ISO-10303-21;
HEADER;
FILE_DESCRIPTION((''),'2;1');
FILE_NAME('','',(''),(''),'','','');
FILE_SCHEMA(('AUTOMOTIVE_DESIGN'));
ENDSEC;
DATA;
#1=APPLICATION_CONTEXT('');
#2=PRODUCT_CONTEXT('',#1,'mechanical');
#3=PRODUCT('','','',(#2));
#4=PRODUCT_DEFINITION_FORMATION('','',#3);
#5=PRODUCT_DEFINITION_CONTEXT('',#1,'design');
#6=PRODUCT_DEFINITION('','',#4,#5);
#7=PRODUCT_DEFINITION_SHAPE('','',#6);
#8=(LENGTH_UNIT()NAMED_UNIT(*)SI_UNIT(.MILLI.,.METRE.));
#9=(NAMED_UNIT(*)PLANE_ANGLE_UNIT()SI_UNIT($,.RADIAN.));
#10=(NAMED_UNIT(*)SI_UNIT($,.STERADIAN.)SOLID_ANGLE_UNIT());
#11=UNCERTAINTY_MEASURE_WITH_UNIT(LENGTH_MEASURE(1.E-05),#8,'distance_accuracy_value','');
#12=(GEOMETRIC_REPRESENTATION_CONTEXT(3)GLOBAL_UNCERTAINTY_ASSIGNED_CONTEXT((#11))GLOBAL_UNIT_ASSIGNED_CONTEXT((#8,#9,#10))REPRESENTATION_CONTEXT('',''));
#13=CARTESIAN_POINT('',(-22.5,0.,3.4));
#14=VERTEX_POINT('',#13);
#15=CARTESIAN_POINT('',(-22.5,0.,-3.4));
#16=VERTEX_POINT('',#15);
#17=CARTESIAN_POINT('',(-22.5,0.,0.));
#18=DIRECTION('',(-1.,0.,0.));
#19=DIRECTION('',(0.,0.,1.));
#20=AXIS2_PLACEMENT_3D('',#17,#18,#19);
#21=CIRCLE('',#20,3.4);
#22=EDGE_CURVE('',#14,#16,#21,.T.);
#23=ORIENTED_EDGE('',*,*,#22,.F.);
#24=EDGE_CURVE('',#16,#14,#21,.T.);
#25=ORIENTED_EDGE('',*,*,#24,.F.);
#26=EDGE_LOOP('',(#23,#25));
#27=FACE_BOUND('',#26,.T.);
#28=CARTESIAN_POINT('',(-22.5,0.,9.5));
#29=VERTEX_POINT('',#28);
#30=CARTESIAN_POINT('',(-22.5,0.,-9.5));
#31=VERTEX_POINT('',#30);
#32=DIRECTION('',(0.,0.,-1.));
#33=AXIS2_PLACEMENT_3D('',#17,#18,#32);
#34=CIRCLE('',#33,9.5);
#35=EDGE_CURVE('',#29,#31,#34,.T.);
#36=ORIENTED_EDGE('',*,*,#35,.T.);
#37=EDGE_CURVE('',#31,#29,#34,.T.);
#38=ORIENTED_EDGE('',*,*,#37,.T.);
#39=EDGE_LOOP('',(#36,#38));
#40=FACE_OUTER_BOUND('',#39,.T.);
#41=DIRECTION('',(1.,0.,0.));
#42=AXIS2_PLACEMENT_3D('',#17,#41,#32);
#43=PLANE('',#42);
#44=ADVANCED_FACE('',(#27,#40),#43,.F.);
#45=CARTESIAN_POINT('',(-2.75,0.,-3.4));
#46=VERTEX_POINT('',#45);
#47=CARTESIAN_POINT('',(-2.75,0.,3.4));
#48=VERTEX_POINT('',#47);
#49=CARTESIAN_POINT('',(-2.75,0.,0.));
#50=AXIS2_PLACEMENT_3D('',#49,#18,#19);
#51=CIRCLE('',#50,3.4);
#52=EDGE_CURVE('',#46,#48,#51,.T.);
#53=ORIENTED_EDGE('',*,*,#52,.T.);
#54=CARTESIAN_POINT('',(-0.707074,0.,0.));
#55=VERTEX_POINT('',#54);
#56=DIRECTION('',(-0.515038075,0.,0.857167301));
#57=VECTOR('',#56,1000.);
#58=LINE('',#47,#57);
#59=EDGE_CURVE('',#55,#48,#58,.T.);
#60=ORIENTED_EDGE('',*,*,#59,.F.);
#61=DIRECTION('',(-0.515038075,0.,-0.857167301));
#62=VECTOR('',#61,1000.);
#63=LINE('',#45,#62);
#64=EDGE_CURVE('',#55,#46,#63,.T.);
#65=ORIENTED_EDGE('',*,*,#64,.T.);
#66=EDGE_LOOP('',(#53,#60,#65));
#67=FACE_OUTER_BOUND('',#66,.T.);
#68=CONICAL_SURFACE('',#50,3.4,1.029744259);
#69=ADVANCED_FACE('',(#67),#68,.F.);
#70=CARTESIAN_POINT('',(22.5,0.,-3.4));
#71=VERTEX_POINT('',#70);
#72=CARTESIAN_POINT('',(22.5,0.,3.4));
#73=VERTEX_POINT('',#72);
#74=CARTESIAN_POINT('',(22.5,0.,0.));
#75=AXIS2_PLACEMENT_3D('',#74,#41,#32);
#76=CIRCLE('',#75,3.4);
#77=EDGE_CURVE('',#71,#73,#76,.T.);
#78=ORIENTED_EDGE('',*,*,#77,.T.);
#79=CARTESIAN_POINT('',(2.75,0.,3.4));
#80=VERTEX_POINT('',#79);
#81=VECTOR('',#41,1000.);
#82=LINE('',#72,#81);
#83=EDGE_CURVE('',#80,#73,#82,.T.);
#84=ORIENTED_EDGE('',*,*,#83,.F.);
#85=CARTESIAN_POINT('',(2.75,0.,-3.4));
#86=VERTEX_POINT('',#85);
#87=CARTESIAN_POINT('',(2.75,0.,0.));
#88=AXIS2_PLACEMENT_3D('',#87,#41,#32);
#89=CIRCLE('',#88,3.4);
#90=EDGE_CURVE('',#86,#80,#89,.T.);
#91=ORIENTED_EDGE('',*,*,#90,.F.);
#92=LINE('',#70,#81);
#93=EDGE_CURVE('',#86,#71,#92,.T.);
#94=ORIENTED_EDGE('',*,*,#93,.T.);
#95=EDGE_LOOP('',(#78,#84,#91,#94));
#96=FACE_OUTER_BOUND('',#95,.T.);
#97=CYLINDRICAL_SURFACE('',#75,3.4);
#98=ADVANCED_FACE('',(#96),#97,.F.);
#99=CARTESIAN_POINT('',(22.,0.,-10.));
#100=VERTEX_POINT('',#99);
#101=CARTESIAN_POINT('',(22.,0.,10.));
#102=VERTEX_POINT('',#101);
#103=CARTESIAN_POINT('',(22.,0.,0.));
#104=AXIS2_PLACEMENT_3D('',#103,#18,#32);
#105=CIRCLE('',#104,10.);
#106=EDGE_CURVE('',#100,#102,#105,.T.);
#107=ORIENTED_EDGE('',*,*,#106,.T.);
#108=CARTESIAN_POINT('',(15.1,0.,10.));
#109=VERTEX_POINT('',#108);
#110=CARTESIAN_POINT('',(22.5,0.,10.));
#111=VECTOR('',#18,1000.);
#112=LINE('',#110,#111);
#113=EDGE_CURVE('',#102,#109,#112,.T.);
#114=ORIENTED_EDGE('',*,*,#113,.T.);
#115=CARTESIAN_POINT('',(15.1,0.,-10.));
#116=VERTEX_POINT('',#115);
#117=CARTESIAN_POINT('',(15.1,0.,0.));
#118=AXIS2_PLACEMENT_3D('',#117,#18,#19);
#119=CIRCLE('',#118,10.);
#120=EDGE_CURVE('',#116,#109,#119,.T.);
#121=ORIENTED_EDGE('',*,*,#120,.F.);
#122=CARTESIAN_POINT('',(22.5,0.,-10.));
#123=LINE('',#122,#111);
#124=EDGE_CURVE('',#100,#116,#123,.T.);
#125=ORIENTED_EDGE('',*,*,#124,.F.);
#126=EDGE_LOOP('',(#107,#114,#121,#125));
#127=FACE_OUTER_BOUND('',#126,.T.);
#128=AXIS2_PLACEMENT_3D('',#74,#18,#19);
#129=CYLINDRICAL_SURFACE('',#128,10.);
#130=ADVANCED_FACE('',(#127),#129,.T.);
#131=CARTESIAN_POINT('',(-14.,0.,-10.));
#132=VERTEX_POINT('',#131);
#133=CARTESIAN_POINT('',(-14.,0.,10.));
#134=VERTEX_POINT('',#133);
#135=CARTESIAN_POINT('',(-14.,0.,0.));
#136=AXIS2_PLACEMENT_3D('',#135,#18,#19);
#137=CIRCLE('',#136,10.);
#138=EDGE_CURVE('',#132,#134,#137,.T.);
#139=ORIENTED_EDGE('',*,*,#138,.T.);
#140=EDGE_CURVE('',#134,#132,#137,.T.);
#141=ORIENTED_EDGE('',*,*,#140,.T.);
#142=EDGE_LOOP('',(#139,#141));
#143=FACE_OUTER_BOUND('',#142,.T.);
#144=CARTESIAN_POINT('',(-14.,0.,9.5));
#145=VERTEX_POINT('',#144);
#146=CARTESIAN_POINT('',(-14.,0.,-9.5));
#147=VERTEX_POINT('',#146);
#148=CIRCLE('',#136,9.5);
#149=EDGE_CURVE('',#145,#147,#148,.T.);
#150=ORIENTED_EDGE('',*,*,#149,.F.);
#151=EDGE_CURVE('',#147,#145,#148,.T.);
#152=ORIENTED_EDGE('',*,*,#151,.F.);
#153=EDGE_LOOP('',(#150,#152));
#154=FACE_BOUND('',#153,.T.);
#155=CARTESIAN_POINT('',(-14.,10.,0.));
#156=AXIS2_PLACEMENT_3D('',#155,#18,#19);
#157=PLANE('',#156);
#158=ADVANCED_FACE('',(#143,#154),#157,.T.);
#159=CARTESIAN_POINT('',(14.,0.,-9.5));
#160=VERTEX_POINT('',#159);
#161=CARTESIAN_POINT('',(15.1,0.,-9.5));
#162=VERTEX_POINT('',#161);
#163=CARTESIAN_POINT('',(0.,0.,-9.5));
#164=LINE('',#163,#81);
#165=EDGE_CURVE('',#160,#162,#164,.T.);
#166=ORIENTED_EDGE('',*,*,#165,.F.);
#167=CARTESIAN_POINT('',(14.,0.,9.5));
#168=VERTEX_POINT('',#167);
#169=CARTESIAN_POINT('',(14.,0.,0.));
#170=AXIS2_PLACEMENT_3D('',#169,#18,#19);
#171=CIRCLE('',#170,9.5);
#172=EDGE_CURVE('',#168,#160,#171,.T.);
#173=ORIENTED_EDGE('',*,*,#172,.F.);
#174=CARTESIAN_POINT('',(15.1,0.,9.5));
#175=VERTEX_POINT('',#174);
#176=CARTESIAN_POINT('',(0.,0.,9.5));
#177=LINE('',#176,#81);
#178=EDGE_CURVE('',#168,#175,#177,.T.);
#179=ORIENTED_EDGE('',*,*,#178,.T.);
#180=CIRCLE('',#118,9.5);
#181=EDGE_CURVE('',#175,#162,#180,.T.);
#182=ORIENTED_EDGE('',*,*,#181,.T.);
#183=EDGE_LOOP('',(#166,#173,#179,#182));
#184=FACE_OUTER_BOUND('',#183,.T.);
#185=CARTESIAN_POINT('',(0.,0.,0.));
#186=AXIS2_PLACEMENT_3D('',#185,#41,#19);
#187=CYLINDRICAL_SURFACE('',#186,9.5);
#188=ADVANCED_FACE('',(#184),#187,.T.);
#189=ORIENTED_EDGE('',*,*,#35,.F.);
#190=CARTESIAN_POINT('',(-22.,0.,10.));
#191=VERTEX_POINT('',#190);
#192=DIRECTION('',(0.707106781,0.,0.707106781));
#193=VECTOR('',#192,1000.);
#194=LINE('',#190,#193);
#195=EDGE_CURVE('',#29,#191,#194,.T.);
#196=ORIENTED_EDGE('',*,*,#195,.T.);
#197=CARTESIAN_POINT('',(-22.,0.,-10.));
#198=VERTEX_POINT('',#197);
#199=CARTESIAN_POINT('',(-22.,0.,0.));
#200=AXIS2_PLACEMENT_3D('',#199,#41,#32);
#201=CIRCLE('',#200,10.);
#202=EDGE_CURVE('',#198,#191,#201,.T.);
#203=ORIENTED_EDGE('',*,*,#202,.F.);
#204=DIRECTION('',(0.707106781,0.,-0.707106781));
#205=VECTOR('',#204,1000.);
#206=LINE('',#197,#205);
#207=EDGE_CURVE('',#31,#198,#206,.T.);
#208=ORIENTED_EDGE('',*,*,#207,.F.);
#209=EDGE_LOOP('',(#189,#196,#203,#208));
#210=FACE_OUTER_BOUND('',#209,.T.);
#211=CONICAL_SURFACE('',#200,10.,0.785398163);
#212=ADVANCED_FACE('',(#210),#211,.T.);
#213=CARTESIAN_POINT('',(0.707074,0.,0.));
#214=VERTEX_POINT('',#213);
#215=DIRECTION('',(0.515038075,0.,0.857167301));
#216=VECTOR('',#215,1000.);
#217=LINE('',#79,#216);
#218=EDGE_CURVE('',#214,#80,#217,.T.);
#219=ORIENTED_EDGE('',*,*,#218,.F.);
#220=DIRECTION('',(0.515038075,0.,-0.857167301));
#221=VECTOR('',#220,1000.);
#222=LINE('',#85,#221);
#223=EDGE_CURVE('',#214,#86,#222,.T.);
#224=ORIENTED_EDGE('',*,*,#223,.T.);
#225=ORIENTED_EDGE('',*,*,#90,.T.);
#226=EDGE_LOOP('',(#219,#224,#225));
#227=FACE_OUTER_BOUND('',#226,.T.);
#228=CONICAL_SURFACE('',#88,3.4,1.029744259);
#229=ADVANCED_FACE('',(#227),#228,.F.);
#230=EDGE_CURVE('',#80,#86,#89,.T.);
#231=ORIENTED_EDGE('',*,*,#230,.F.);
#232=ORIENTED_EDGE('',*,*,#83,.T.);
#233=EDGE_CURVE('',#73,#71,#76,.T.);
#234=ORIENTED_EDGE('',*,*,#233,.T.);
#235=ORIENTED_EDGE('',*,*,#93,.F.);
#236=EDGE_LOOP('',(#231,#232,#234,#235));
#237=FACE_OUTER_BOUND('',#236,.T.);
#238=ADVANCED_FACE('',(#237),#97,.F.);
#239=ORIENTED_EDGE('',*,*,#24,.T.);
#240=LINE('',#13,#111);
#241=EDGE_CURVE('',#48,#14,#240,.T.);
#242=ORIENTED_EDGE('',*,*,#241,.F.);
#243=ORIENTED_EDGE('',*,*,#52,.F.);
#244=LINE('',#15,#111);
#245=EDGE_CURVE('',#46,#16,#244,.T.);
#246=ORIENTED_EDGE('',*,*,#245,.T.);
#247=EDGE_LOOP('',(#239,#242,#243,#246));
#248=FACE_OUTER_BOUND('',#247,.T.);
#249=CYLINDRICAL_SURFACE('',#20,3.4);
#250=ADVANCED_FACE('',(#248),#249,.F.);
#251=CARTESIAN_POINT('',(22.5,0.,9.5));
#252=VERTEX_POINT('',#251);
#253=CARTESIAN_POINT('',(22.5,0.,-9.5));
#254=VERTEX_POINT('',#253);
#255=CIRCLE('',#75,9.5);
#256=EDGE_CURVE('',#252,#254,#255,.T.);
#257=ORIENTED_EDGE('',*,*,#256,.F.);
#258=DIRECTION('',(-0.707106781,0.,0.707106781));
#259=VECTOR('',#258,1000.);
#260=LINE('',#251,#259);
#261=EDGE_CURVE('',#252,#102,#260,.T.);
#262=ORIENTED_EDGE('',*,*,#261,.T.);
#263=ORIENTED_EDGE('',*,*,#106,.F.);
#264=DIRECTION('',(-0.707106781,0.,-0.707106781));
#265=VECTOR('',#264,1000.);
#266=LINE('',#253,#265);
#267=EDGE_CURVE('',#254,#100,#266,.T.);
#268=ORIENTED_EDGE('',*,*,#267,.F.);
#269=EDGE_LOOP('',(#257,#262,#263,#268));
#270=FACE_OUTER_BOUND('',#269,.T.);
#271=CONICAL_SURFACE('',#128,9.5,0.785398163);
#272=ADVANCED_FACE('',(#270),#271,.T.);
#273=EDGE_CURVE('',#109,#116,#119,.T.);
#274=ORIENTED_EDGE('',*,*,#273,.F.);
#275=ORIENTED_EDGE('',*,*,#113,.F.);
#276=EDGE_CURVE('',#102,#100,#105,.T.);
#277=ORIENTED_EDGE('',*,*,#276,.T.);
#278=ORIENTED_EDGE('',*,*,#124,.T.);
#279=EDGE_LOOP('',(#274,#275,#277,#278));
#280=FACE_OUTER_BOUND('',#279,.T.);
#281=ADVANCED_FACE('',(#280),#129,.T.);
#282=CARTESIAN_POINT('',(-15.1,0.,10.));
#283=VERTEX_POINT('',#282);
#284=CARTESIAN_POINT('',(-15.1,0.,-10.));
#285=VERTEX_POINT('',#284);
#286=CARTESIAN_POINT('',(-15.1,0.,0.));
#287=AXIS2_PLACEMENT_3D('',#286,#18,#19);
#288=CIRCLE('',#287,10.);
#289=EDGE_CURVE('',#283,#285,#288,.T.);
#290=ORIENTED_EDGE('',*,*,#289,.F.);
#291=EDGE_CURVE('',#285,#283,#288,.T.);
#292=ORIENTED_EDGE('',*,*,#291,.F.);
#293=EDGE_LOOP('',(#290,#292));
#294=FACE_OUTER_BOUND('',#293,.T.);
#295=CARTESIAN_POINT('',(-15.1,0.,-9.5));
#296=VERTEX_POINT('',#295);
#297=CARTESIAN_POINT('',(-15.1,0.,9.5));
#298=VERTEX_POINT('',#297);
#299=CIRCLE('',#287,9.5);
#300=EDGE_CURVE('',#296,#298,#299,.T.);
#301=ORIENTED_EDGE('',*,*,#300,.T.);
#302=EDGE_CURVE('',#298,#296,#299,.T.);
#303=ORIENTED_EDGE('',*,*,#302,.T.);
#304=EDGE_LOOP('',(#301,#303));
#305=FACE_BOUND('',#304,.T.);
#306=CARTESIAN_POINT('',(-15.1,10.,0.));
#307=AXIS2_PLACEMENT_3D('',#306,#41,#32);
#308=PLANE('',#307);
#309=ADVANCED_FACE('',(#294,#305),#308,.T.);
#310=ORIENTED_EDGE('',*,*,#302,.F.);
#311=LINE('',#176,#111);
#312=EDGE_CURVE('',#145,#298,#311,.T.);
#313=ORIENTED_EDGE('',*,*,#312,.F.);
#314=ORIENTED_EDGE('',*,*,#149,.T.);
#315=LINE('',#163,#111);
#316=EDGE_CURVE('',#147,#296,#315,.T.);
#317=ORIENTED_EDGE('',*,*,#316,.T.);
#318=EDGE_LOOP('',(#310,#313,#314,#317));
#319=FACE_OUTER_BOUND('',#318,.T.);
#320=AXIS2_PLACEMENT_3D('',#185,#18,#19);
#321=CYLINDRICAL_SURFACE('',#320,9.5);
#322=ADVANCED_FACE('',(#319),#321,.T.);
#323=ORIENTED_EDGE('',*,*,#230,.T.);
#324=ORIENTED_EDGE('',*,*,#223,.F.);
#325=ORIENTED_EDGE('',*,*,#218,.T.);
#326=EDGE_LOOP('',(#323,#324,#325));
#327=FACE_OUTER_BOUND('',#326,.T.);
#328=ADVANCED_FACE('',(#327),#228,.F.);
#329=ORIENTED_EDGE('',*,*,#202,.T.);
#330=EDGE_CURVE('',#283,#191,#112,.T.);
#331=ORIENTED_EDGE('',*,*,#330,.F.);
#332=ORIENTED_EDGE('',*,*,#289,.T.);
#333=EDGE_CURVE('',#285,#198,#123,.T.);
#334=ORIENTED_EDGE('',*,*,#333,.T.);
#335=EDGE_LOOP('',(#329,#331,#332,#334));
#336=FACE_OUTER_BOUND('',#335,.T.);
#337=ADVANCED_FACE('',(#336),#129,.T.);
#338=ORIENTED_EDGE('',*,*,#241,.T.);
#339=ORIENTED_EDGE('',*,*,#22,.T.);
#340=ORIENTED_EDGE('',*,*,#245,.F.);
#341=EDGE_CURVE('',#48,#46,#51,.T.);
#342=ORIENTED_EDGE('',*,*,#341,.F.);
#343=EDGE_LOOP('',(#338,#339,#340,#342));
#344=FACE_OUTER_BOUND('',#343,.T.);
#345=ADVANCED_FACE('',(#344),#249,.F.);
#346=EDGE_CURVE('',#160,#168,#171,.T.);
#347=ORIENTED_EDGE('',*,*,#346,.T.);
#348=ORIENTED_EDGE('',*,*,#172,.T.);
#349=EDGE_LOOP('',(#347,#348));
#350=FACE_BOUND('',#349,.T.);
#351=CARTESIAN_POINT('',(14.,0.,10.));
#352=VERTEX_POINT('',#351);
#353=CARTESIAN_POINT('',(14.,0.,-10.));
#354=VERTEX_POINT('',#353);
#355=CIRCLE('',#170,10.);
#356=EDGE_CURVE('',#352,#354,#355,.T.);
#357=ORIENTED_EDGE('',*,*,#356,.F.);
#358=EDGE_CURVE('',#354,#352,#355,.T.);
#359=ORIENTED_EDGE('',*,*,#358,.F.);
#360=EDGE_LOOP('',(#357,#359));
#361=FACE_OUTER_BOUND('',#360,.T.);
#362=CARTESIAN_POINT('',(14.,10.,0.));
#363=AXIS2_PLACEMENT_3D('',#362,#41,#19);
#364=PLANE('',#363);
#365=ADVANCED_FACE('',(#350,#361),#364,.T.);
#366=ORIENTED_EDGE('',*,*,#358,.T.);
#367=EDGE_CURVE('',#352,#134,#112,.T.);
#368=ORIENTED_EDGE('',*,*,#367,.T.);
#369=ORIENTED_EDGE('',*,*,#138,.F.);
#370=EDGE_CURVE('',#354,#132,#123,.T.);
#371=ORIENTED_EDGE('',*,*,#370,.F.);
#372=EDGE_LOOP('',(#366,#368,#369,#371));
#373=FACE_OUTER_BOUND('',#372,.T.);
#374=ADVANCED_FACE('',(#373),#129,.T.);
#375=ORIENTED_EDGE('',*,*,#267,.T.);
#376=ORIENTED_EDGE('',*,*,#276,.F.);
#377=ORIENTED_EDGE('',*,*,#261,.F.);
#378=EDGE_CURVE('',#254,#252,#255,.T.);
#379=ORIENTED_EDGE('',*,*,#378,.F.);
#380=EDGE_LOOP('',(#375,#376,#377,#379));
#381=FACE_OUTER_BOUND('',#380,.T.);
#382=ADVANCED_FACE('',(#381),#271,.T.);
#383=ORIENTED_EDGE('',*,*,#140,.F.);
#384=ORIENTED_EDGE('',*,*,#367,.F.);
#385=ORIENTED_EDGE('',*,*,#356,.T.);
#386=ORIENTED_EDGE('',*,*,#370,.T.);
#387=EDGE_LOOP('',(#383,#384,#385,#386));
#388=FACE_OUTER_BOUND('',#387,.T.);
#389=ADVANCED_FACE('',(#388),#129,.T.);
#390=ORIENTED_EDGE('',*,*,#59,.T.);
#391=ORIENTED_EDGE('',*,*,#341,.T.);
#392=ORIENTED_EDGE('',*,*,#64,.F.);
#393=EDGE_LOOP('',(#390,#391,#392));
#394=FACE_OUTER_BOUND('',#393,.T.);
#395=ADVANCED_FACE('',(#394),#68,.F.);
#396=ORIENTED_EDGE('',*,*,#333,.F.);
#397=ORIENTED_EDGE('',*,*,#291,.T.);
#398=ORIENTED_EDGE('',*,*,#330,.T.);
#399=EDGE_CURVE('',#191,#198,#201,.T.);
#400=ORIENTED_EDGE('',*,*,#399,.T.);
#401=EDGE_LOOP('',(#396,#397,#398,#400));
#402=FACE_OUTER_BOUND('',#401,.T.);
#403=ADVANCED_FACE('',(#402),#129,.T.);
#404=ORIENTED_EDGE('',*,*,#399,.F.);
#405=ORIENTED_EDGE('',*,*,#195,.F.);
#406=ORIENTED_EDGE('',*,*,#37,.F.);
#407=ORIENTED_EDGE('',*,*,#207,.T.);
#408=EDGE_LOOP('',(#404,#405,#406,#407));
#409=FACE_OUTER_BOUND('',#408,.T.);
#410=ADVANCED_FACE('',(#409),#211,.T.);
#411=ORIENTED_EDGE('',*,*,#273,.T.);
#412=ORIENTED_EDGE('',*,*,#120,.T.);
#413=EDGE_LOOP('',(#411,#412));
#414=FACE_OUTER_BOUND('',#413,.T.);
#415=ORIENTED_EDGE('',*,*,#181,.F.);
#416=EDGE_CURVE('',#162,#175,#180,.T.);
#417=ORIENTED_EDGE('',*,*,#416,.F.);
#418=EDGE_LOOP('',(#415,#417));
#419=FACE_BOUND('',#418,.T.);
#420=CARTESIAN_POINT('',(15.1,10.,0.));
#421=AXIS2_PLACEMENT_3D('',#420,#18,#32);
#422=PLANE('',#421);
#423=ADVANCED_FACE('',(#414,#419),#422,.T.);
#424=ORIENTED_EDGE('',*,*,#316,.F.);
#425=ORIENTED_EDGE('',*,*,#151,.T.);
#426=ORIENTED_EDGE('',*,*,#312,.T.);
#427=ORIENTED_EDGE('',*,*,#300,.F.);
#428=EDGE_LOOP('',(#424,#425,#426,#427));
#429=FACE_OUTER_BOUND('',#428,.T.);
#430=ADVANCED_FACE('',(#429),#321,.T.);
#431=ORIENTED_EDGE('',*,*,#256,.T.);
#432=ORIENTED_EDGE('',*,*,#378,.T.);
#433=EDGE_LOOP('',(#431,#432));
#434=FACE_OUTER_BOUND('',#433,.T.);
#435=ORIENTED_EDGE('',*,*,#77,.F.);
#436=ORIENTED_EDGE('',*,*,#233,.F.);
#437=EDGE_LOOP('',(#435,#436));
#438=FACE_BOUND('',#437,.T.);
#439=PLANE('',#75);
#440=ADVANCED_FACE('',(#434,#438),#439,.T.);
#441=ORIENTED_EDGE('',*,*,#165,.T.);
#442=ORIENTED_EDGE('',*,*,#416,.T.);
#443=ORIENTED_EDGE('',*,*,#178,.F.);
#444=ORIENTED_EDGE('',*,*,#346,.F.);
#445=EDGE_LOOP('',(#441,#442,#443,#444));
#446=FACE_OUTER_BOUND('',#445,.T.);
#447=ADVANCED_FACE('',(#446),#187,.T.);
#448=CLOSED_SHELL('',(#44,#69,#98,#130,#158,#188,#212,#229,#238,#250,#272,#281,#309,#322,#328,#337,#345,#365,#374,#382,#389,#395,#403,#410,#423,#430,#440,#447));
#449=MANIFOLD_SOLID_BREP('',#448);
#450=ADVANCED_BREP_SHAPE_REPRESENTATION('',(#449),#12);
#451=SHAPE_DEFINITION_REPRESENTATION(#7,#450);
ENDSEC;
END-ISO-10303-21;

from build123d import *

# Parameters (mm, degrees)
SKETCH_1_R      = 10
EXTRUDE_1_DEPTH = 22.5
CHAMFER_1_SIZE  = 0.5
SKETCH_4_W      = 1.1
SKETCH_4_H      = 0.5


with BuildPart() as part:
    # 草图1 → 凸台-拉伸1 (new, symmetric)
    with BuildSketch(Plane(origin=(0, 0, 0), x_dir=(0, 0, -1), z_dir=(1, 0, 0))):
        with Locations(Location((0, 0, 0), (0, 0, 180))):
            Circle(SKETCH_1_R)
    extrude(amount=EXTRUDE_1_DEPTH, both=True)

    # 草图2 → M8 螺纹孔1 (revolve, cut)
    with BuildSketch(Plane(origin=(22.5, 0, 0), x_dir=(0, 0, -1), z_dir=(0, 1, 0))):
        Polygon((0, 0), (0, 21.792926105), (3.4, 19.75), (3.4, 0), align=None)
    hole_wizard_m8_1 = revolve(axis=Axis((28.85, 0, 0), (-1, 0, 0)), mode=Mode.SUBTRACT)

    # 镜向1: M8 螺纹孔1 across plane
    add(hole_wizard_m8_1.mirror(Plane(origin=(0, 0, 0), x_dir=(0, 0, 1), z_dir=(1, 0, 0))), mode=Mode.SUBTRACT)

    # 倒角1
    chamfer_1_edges = [part.edges().sort_by_distance(p)[0] for p in [
        (-22.5, 0, -10),
        (22.5, 0, -10),
    ]]
    chamfer(chamfer_1_edges, length=CHAMFER_1_SIZE)

    # 草图4 → 切除-旋转1 (revolve, cut)
    with BuildSketch(Plane.XY, mode=Mode.PRIVATE) as cut_revolve_1_sk:
        with Locations((-14.55, 9.75)):
            Rectangle(SKETCH_4_W, SKETCH_4_H)
    cut_revolve_1 = revolve(cut_revolve_1_sk.sketch.rotate(Axis((0, 0, 0), (1, 0, 0)), 90), axis=Axis((0, 0, 0), (1, 0, 0)), mode=Mode.SUBTRACT)

    # 镜向2: 切除-旋转1 across plane
    add(cut_revolve_1.mirror(Plane(origin=(0, 0, 0), x_dir=(0, 0, 1), z_dir=(1, 0, 0))), mode=Mode.SUBTRACT)


solid = part.part
